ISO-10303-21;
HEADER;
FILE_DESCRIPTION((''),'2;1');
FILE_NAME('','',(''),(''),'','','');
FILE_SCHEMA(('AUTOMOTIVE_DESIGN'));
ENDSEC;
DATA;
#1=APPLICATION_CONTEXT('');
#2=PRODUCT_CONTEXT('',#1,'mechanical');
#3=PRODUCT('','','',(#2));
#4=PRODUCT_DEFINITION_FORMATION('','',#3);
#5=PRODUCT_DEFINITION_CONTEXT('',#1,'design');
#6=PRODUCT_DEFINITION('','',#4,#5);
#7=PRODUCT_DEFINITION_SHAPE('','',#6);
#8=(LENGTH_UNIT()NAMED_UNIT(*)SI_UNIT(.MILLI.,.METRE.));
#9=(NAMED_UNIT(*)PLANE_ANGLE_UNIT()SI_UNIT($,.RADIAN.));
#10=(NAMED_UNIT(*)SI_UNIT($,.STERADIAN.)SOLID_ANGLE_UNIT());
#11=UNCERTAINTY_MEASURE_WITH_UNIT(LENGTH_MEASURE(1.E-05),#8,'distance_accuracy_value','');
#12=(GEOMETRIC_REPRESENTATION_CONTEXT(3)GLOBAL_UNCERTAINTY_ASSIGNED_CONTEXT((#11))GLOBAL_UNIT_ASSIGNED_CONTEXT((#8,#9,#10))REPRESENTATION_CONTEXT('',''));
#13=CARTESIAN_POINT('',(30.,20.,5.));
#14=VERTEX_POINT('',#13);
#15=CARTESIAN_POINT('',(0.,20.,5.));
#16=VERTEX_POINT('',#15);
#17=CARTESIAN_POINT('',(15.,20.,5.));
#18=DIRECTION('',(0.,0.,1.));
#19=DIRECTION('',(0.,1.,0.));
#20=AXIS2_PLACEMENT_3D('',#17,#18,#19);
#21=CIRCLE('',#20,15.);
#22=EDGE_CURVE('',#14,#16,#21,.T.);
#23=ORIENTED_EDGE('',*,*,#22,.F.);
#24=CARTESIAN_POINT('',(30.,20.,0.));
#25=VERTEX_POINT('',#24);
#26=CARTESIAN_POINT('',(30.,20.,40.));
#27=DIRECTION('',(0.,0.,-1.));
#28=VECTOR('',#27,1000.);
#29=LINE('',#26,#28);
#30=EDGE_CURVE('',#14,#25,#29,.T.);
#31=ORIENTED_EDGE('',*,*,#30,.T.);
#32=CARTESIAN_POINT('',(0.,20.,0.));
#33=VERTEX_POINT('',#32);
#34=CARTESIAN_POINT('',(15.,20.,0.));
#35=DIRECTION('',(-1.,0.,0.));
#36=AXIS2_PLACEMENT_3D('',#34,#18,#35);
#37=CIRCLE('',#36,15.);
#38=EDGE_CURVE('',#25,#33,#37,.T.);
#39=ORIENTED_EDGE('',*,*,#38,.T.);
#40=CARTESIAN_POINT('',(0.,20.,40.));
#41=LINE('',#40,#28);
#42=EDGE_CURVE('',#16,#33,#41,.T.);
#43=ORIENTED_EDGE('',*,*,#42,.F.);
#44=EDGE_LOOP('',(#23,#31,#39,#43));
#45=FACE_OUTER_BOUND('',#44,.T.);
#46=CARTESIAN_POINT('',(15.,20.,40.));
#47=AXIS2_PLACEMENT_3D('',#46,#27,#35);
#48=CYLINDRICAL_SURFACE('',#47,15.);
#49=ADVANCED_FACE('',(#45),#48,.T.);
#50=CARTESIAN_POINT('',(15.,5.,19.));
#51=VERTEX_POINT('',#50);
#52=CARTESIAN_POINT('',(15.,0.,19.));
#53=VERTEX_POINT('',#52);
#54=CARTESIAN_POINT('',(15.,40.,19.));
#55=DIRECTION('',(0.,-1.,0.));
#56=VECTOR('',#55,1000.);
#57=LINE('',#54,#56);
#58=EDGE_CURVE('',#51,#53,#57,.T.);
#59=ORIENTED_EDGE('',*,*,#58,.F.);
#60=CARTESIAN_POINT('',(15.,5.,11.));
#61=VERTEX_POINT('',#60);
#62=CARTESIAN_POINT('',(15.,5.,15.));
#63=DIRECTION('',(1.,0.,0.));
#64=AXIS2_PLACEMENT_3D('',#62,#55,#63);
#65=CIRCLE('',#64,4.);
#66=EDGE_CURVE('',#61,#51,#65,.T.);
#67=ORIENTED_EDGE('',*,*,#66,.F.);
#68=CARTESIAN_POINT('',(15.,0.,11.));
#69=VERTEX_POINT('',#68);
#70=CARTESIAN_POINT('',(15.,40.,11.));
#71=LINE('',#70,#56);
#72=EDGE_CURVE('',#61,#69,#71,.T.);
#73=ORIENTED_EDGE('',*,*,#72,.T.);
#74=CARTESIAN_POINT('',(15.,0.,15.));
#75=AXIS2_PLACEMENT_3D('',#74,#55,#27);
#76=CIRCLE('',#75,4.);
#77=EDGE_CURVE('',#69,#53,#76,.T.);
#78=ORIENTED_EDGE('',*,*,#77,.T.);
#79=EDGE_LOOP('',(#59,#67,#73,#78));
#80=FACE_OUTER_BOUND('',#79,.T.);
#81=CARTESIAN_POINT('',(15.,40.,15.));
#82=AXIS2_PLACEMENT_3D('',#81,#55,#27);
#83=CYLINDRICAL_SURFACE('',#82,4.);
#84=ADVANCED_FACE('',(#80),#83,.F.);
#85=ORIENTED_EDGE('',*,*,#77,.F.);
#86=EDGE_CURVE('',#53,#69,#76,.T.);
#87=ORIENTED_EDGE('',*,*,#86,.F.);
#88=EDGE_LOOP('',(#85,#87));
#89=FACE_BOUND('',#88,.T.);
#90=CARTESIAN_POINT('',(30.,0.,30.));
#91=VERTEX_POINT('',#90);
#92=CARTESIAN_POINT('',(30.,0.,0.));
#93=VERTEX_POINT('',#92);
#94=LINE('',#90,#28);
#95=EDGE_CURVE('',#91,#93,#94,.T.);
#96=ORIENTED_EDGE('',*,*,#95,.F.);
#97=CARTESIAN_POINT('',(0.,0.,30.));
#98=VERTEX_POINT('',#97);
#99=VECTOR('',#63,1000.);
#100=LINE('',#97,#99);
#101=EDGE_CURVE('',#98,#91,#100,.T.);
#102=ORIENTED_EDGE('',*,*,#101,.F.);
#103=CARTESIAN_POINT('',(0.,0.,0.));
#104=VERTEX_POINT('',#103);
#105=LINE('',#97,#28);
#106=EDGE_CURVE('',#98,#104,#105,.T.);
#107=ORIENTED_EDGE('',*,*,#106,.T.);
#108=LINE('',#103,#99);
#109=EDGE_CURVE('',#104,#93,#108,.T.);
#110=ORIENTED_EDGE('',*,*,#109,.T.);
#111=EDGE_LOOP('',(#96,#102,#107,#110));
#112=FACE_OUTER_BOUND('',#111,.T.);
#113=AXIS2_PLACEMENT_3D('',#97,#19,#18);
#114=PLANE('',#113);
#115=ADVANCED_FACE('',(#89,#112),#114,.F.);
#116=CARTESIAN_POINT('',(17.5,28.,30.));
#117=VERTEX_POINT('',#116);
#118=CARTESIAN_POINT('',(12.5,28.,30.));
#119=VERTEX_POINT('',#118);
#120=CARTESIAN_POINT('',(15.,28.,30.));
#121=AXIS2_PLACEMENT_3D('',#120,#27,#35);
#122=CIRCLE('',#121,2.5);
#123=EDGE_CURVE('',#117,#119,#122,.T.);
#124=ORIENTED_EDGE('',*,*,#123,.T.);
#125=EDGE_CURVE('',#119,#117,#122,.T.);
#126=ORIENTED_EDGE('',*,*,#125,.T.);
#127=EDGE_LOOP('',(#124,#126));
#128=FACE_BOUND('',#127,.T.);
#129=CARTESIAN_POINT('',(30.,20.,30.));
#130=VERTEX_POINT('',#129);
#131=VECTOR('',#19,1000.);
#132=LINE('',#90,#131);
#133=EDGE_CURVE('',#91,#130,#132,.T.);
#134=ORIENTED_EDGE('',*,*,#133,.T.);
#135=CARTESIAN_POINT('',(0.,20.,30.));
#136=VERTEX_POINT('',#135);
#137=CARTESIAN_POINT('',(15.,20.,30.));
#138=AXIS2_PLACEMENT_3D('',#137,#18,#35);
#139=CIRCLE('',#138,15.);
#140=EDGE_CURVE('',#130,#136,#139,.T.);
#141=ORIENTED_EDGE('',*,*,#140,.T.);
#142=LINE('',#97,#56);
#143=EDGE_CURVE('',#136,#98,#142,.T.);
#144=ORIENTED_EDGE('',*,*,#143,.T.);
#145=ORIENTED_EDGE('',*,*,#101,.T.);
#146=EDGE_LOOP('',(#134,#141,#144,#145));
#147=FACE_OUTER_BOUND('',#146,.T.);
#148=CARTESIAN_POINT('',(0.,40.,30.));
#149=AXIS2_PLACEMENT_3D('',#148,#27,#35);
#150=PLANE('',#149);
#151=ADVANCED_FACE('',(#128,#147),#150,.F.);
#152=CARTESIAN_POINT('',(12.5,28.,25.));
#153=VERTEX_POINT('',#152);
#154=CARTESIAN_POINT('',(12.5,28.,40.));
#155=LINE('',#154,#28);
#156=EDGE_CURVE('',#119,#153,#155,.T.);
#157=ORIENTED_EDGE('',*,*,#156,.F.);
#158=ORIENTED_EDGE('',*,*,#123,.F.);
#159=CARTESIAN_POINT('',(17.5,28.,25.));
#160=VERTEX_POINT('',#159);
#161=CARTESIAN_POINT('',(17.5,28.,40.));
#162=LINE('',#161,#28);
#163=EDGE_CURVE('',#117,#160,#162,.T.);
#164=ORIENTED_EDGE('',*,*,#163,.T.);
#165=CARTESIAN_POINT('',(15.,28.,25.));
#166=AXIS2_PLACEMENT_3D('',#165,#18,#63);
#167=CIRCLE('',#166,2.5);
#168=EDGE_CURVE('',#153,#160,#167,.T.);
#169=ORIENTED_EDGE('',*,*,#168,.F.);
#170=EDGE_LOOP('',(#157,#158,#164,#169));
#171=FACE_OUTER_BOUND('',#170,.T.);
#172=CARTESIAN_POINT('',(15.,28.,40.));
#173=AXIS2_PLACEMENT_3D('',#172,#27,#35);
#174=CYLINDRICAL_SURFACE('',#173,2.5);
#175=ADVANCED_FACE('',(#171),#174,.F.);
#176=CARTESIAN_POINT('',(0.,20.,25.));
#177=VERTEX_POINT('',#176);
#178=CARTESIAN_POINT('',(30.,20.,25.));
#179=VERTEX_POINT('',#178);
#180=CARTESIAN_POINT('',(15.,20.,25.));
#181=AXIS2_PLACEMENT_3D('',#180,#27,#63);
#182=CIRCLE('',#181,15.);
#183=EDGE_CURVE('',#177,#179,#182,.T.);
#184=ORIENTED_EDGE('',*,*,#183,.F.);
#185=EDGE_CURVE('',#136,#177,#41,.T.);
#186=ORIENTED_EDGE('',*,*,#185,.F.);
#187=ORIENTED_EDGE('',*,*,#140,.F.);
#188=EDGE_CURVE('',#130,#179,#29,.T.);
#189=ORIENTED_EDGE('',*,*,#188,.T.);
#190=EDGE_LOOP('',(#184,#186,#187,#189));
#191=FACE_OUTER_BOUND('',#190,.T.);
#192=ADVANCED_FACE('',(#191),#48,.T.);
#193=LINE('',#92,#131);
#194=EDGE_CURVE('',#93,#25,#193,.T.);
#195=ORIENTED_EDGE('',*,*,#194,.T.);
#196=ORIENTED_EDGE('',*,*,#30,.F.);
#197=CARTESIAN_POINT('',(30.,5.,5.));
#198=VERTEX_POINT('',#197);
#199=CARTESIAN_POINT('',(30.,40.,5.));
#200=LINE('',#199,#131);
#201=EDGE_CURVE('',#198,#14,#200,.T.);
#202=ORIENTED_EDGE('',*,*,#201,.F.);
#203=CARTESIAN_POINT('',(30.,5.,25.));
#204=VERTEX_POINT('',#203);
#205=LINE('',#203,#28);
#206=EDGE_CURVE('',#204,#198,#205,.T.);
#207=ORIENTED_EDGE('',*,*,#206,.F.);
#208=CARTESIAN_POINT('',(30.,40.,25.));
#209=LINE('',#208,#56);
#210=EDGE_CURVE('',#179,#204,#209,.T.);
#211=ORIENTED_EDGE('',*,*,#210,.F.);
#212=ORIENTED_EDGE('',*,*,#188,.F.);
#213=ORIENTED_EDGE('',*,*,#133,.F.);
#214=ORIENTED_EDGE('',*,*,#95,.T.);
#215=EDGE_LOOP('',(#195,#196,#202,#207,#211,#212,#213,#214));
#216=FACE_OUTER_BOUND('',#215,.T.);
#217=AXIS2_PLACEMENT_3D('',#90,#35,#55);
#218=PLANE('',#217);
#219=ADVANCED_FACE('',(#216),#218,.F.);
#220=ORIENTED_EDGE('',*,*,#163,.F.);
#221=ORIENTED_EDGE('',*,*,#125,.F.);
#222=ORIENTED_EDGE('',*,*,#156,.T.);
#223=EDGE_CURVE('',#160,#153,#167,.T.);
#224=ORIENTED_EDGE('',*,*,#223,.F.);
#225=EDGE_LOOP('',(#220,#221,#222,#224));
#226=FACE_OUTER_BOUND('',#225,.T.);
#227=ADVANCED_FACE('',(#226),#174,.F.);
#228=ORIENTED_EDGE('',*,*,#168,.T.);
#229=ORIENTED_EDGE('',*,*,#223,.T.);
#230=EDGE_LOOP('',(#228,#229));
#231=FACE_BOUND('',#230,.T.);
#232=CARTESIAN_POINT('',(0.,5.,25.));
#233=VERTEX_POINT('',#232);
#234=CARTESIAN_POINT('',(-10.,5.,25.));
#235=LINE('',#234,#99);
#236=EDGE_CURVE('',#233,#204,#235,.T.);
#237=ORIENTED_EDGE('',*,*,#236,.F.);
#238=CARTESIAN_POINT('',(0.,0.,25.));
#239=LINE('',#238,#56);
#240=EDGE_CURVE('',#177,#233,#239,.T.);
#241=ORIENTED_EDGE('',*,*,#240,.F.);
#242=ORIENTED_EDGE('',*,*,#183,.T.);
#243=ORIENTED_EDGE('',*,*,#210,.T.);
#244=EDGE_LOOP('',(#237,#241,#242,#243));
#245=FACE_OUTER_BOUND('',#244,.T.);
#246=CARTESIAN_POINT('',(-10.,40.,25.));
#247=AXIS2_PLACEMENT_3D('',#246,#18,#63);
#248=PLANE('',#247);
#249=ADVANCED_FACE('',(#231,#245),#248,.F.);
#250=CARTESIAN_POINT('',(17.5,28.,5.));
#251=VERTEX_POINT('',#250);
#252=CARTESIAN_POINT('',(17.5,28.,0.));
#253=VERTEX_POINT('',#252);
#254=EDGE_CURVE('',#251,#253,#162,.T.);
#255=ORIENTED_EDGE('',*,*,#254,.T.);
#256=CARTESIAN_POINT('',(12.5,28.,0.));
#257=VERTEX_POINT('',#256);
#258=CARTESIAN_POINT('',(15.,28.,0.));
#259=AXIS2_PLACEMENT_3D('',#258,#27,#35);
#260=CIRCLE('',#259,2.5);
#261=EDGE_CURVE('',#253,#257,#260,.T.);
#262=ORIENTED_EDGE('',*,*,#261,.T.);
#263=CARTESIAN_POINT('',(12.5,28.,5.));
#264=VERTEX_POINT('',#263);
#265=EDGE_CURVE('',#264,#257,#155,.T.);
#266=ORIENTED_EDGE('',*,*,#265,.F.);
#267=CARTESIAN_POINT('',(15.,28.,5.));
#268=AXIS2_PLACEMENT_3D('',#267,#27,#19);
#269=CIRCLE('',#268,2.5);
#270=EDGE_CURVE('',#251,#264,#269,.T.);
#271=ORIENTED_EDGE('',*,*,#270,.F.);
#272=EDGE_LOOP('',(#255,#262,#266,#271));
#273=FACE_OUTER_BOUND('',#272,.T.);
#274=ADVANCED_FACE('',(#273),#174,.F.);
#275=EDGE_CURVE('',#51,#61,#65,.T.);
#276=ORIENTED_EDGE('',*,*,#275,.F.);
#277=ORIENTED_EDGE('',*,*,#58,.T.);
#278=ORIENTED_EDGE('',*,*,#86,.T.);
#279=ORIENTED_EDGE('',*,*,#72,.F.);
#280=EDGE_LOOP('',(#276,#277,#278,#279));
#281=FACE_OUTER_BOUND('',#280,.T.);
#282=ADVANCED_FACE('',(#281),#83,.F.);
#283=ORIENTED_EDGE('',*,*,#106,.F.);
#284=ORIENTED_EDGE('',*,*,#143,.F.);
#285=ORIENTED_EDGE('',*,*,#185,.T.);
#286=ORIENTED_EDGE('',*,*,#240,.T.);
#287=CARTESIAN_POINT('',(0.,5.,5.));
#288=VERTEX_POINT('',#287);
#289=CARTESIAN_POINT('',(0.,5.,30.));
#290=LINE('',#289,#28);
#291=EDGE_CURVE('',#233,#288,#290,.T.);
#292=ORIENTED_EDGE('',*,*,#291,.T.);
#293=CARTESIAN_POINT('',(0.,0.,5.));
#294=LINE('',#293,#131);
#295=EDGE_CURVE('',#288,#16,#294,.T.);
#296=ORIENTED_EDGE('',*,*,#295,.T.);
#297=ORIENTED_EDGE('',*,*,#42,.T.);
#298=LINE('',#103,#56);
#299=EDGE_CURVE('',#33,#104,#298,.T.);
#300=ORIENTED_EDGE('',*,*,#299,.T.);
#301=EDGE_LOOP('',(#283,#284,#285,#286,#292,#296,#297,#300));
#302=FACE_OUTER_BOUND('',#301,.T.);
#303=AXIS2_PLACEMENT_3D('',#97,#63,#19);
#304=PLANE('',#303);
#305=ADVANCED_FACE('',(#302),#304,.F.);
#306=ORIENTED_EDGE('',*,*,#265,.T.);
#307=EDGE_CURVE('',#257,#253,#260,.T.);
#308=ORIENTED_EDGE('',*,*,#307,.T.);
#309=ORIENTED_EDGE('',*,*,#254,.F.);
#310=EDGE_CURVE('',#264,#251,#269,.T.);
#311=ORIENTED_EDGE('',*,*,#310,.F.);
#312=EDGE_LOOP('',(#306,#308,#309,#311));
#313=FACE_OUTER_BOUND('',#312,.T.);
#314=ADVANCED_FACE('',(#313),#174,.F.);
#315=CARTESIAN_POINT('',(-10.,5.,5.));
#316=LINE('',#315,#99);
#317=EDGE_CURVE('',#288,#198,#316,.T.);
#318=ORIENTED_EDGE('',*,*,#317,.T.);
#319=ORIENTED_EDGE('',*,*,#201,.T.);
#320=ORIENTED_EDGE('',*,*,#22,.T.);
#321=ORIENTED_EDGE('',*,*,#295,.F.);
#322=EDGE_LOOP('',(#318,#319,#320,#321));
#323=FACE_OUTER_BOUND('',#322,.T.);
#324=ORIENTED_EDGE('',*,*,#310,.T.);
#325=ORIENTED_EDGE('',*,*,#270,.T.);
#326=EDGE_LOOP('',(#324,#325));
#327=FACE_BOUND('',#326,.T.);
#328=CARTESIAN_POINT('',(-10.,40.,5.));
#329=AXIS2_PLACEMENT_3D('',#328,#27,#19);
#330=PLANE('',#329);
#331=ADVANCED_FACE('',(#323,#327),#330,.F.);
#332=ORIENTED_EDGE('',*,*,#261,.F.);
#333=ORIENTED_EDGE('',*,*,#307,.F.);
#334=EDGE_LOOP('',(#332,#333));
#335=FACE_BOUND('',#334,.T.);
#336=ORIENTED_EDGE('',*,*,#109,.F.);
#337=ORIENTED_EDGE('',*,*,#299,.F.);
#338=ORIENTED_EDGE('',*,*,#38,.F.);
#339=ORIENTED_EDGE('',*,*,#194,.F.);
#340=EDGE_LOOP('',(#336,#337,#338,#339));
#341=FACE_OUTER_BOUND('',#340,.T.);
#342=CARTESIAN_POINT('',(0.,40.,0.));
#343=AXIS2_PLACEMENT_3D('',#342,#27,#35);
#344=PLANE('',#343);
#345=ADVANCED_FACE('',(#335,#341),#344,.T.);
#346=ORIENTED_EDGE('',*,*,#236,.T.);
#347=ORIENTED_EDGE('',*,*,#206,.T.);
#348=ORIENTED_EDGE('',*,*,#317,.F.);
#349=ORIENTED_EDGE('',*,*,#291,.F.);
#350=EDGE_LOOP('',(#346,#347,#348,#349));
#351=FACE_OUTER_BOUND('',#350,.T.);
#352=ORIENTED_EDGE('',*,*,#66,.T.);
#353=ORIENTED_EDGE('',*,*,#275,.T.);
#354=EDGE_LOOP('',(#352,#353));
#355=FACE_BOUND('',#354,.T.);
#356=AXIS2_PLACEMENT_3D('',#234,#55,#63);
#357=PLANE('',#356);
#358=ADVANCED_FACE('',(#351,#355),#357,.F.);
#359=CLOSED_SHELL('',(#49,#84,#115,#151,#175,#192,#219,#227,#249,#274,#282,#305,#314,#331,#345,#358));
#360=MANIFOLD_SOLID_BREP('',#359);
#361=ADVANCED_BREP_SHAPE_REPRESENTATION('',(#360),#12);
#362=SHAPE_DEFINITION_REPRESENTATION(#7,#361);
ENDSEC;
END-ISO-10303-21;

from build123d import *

# Parameters (mm, degrees)
SKETCH_1_W          = 30
SKETCH_1_H          = 40
EXTRUDE_1_DEPTH     = 30
SKETCH_4_W          = 20
SKETCH_4_H          = 35
CUT_EXTRUDE_1_DEPTH = 40
CUT_EXTRUDE_2_DEPTH = 40
SKETCH_6_R          = 2.5
CUT_EXTRUDE_3_DEPTH = 40
SKETCH_7_R          = 4
CUT_EXTRUDE_4_DEPTH = 40


with BuildPart() as part:
    # 草图1 → 凸台-拉伸1 (new body)
    with BuildSketch(Plane.XY):
        with Locations((15, 20)):
            Rectangle(SKETCH_1_W, SKETCH_1_H)
    extrude(amount=EXTRUDE_1_DEPTH)

    # 草图4 → 切除-拉伸1 (cut)
    with BuildSketch(Plane(origin=(30, 0, 0), x_dir=(0, 0, -1), z_dir=(1, 0, 0))):
        with Locations((-15, 22.5)):
            Rectangle(SKETCH_4_W, SKETCH_4_H)
    extrude(amount=-CUT_EXTRUDE_1_DEPTH, mode=Mode.SUBTRACT)

    # 草图5 → 切除-拉伸2 (cut)
    with BuildSketch(Plane(origin=(0, 0, 0), x_dir=(-1, 0, 0), z_dir=(0, 0, -1))):
        with BuildLine():
            Line((-30, 20), (-30, 40))
            Line((-30, 40), (0, 40))
            Line((0, 40), (0, 20))
            ThreePointArc((0, 20), (-15, 35), (-30, 20))
        make_face()
    extrude(amount=-CUT_EXTRUDE_2_DEPTH, mode=Mode.SUBTRACT)

    # 草图6 → 切除-拉伸3 (cut)
    with BuildSketch(Plane(origin=(0, 0, 0), x_dir=(-1, 0, 0), z_dir=(0, 0, -1))):
        with Locations((-15, 28)):
            Circle(SKETCH_6_R)
    extrude(amount=-CUT_EXTRUDE_3_DEPTH, mode=Mode.SUBTRACT)

    # 草图7 → 切除-拉伸4 (cut)
    with BuildSketch(Plane.XZ):
        with Locations(Location((15, 15, 0), (0, 0, 270))):
            Circle(SKETCH_7_R)
    extrude(amount=-CUT_EXTRUDE_4_DEPTH, mode=Mode.SUBTRACT)


solid = part.part
